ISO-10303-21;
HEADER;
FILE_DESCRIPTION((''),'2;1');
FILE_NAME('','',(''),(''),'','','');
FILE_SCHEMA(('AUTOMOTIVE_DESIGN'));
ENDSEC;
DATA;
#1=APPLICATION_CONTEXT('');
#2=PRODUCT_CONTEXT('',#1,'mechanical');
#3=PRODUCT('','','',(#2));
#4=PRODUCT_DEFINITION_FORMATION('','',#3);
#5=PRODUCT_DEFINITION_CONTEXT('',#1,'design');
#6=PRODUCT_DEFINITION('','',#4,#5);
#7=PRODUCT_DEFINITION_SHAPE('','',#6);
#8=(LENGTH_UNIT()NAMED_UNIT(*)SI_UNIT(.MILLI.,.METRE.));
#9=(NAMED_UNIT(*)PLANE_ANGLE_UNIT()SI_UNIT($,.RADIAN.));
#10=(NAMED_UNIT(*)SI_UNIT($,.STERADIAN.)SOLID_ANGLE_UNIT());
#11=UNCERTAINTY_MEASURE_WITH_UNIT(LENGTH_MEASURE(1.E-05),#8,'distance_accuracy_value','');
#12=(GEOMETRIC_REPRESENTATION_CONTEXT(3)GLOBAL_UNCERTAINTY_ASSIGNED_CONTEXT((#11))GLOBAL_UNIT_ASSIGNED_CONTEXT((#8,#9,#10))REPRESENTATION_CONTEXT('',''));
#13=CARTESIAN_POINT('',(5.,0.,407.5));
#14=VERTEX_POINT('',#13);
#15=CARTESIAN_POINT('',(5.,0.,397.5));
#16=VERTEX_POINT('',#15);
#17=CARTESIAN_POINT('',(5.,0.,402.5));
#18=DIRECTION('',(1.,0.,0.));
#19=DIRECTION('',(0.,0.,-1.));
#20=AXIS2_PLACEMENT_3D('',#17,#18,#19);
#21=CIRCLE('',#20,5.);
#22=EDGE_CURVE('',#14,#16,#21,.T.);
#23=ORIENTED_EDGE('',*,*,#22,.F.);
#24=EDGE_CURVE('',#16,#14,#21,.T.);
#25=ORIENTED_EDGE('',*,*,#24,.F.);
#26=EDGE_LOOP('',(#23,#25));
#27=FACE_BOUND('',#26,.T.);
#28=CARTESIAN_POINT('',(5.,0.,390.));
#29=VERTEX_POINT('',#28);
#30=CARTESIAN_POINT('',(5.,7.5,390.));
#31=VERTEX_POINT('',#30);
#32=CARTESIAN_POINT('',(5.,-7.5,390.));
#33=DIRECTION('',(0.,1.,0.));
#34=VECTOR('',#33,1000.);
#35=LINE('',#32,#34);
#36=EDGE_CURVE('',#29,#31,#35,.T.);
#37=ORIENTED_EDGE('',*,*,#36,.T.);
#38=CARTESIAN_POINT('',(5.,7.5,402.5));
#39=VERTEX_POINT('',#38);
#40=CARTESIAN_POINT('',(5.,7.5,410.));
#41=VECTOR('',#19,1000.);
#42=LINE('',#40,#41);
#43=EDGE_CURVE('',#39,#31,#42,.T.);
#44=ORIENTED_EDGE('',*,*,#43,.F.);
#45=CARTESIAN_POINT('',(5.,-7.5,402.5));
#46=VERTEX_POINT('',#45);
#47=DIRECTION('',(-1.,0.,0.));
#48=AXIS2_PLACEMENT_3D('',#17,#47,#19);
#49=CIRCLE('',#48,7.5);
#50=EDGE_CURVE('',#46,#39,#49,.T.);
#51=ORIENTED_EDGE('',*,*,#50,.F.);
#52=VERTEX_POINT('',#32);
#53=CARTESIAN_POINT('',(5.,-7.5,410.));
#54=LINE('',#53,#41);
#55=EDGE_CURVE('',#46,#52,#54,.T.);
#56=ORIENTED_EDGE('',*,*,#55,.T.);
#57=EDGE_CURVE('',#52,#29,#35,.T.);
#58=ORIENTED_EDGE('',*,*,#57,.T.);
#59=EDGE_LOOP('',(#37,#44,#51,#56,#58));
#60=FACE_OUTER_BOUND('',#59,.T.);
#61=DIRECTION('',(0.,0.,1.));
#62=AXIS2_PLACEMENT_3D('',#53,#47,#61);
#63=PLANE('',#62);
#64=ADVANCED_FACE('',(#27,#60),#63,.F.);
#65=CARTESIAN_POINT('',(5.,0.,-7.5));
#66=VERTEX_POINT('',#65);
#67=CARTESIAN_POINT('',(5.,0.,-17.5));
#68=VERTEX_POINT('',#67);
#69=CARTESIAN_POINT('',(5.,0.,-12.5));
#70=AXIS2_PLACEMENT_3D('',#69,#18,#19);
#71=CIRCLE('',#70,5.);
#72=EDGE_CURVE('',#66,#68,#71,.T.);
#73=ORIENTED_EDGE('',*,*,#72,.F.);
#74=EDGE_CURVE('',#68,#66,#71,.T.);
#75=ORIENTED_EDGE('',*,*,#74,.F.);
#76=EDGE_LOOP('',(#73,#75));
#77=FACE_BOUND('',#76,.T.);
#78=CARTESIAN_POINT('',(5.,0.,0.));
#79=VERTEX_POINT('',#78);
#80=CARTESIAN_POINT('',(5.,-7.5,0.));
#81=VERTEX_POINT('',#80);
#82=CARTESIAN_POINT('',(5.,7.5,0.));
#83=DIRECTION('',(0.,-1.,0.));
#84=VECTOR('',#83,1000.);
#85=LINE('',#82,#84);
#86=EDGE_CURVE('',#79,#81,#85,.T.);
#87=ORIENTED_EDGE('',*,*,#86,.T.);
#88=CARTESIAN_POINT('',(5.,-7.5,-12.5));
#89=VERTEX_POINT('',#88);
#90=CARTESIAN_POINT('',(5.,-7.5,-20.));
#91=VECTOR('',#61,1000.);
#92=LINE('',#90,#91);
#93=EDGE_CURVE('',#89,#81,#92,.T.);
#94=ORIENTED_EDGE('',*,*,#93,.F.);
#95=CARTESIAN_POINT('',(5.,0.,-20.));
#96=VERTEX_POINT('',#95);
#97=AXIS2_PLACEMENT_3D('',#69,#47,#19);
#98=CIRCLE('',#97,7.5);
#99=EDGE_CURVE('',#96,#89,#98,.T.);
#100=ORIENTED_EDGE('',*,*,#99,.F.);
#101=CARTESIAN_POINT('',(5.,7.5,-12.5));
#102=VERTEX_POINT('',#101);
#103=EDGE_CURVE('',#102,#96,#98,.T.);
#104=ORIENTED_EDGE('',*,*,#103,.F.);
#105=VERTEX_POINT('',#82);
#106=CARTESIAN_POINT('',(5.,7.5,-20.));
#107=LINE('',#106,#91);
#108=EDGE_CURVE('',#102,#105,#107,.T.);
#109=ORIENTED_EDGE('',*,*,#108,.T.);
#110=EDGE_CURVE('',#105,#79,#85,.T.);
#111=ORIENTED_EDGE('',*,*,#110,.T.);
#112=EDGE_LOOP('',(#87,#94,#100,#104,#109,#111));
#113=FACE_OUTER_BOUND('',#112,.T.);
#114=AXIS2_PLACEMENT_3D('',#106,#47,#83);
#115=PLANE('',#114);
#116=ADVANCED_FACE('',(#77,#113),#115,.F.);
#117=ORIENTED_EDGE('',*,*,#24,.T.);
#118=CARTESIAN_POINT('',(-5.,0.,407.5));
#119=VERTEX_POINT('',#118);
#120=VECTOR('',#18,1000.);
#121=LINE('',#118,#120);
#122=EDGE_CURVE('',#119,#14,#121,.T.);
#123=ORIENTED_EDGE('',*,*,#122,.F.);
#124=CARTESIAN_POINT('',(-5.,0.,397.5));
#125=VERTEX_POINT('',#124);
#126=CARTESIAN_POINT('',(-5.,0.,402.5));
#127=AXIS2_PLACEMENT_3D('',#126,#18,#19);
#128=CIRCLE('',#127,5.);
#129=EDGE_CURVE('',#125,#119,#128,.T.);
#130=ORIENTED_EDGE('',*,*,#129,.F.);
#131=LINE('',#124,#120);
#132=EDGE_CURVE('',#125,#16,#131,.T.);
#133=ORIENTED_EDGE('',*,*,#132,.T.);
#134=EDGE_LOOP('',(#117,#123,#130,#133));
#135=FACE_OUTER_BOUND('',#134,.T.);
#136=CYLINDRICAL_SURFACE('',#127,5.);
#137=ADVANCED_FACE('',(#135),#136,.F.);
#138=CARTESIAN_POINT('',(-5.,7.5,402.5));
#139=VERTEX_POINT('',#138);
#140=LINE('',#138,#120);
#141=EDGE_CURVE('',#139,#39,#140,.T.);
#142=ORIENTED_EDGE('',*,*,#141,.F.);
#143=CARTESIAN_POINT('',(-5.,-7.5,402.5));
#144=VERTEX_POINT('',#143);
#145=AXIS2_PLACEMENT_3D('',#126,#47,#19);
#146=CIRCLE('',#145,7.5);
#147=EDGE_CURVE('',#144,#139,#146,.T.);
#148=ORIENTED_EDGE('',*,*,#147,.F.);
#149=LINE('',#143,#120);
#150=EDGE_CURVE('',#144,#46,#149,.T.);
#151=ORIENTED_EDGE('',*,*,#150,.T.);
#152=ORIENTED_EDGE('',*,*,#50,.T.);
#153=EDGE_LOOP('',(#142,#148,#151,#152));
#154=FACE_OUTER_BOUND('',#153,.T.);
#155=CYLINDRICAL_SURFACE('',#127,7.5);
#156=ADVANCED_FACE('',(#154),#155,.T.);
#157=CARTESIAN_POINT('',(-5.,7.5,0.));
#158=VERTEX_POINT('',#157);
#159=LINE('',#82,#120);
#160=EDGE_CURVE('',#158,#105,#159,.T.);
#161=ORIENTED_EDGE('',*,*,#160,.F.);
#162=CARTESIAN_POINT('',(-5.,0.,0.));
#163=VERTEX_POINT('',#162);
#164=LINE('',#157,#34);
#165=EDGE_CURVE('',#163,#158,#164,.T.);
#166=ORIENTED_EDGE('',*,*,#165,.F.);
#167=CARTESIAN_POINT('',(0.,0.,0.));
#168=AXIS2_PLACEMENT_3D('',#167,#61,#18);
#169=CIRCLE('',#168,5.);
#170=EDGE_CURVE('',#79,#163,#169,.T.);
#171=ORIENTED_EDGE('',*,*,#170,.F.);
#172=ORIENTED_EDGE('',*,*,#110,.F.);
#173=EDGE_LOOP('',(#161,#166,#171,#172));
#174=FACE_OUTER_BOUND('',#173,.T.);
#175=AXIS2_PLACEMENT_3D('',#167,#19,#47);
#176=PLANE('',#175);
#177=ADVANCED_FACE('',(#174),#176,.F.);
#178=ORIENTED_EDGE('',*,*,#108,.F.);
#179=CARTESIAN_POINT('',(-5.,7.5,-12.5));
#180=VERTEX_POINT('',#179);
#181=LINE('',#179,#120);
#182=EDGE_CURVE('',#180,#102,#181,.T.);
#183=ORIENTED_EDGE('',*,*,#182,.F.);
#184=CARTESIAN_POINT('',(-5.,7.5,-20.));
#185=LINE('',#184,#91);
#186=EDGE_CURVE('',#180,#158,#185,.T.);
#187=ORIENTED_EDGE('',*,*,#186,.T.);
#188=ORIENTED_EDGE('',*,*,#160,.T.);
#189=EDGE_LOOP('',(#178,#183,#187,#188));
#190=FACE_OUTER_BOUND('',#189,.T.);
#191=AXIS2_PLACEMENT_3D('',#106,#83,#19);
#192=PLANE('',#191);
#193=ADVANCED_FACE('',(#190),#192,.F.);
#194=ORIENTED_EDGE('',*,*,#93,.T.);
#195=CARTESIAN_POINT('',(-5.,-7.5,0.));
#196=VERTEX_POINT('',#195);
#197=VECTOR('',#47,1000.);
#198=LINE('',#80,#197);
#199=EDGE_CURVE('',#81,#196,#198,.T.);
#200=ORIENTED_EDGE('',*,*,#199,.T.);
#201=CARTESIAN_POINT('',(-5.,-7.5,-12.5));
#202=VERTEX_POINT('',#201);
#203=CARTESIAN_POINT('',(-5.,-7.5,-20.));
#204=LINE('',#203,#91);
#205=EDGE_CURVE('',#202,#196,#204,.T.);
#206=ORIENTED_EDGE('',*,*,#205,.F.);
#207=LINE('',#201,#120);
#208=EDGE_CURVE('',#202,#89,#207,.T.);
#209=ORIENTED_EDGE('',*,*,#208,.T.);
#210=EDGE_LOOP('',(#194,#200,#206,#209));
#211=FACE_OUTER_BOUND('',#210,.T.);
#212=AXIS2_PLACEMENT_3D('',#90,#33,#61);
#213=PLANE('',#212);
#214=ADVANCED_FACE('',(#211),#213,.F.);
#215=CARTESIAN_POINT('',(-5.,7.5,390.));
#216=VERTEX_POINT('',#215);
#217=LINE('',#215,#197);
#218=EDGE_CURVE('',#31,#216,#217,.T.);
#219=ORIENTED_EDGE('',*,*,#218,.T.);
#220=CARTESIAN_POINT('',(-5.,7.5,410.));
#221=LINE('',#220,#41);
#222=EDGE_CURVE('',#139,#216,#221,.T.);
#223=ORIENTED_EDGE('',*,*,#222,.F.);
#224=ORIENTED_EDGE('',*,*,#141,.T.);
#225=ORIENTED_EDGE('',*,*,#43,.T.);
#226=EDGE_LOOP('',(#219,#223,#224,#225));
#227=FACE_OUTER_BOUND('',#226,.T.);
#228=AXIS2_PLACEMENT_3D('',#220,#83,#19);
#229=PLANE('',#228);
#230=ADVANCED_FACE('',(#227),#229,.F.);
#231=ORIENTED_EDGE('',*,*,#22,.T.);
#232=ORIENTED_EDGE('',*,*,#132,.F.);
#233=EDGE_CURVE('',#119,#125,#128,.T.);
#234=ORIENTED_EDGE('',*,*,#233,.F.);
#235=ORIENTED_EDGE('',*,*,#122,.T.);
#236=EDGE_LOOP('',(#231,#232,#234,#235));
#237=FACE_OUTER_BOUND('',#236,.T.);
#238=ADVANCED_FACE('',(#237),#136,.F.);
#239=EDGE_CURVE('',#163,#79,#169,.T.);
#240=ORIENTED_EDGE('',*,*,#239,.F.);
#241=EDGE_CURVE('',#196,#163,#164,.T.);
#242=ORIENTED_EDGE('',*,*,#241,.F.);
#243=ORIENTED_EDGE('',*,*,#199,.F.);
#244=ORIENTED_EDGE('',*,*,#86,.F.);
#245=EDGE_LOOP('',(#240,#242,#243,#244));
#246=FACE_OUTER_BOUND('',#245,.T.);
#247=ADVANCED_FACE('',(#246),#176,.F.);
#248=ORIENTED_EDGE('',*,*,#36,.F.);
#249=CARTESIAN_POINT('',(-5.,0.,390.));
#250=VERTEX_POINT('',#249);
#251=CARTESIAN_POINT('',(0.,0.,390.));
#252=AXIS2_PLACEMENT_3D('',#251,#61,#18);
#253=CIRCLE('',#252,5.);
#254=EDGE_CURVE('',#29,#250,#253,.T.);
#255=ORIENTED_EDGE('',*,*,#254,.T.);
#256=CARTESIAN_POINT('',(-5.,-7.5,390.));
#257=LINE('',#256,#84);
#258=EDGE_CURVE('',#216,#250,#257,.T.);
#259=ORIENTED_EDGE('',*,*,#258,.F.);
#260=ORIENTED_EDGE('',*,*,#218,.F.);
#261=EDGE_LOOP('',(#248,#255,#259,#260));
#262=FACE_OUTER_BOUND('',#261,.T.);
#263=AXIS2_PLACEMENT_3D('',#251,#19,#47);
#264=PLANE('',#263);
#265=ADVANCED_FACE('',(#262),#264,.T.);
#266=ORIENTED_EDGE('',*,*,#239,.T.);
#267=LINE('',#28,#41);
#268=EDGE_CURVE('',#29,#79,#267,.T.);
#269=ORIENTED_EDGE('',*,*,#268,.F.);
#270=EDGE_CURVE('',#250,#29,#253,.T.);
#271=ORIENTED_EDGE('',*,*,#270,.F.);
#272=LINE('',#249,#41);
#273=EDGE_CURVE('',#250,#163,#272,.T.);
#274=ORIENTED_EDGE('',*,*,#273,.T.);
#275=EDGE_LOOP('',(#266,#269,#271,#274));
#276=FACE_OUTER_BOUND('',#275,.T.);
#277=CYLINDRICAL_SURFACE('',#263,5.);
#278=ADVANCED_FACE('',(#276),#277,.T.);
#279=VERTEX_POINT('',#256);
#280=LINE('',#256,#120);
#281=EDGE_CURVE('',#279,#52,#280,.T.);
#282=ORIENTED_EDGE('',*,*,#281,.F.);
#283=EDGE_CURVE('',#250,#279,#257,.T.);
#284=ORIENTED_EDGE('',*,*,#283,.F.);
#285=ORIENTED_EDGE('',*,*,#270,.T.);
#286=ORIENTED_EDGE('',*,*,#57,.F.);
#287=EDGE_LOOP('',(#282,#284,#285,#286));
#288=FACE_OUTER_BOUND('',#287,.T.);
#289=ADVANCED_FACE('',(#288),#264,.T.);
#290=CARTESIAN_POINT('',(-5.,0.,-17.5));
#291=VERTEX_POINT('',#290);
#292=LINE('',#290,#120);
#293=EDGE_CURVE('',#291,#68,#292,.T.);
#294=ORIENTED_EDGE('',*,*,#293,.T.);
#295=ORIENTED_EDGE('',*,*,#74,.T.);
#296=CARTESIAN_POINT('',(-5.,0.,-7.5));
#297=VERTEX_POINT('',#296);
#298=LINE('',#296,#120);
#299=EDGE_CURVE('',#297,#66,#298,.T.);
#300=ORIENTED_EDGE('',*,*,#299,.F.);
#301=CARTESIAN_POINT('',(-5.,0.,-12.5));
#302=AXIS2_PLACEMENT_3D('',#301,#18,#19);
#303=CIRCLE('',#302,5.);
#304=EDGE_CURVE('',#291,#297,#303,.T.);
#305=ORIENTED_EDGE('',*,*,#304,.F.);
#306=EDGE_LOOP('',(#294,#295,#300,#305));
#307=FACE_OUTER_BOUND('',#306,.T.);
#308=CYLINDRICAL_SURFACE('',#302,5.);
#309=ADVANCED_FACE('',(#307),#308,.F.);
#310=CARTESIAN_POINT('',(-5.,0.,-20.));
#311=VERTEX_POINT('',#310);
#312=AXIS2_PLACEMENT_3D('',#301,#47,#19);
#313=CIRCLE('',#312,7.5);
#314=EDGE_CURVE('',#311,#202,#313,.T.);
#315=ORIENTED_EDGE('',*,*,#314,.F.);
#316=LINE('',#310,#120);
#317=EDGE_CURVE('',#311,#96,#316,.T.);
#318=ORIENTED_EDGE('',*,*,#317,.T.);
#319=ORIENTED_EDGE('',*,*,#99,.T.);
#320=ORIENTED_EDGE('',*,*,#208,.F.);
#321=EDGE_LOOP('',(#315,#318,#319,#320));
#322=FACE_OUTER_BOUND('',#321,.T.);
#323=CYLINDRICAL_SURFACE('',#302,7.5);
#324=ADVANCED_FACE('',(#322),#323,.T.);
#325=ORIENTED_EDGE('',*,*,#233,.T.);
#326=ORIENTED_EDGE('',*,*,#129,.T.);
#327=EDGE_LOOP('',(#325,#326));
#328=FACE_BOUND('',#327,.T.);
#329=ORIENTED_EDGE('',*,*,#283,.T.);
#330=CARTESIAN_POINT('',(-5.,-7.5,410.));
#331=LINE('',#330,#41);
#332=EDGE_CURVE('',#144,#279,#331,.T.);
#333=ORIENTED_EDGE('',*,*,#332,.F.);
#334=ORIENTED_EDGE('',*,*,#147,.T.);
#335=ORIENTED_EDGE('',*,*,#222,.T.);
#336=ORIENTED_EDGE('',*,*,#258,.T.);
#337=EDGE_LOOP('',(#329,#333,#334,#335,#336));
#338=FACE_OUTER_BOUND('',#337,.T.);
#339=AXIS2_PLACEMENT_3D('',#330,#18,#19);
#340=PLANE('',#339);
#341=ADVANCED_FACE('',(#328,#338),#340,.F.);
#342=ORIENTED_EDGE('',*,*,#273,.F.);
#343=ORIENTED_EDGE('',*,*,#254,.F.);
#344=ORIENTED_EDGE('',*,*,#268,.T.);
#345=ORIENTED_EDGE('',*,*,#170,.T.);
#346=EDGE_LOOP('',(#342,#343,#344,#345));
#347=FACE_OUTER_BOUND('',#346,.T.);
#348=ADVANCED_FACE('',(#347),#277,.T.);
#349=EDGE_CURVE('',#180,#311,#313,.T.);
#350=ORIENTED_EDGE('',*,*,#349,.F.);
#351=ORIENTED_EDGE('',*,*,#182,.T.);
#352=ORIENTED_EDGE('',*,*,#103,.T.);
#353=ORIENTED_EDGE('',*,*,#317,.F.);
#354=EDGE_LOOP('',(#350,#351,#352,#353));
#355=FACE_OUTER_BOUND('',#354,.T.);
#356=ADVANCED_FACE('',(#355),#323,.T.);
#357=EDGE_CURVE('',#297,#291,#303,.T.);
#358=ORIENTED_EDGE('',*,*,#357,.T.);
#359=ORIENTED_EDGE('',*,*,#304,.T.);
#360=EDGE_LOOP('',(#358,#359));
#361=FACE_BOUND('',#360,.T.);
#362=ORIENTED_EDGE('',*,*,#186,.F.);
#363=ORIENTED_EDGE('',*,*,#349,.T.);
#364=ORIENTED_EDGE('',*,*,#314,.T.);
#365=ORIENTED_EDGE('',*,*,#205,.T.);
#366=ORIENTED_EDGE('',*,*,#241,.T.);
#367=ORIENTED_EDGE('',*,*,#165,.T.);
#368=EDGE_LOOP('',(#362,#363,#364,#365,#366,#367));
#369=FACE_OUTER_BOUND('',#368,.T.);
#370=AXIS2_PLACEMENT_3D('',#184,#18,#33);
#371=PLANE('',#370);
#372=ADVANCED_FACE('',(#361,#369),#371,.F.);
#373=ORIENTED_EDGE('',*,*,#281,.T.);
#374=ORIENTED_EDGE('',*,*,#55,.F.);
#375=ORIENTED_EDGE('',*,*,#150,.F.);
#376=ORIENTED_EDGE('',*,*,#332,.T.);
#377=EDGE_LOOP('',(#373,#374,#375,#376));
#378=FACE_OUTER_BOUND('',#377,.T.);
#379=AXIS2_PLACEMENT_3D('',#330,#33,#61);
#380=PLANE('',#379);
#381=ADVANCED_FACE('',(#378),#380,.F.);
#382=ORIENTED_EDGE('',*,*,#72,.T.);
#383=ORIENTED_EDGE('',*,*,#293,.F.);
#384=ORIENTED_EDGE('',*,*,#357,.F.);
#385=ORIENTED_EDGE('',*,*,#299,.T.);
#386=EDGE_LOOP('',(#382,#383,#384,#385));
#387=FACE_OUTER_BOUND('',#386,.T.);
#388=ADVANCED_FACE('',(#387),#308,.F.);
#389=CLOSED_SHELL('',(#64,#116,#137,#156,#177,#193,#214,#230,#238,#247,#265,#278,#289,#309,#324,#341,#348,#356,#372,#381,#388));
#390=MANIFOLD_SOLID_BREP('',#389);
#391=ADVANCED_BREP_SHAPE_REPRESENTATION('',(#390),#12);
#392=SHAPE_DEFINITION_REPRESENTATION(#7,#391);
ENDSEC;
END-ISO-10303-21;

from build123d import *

# Parameters (mm, degrees)
SKETCH1_R           = 5
BOSS_EXTRUDE1_DEPTH = 390
SKETCH2_W           = 10
SKETCH2_H           = 15
BOSS_EXTRUDE2_DEPTH = 20
SKETCH3_W           = 10
SKETCH3_H           = 15
BOSS_EXTRUDE3_DEPTH = 20
SKETCH4_R           = 5
CUT_EXTRUDE1_DEPTH  = 411.190504522


with BuildPart() as part:
    # Sketch1 → Boss-Extrude1 (new body)
    with BuildSketch(Plane.XY):
        Circle(SKETCH1_R)
    extrude(amount=BOSS_EXTRUDE1_DEPTH)

    # Sketch2 → Boss-Extrude2 (add)
    with BuildSketch(Plane(origin=(0, 0, 0), x_dir=(-1, 0, 0), z_dir=(0, 0, -1))):
        Rectangle(SKETCH2_W, SKETCH2_H)
    extrude(amount=BOSS_EXTRUDE2_DEPTH)

    # Sketch3 → Boss-Extrude3 (add)
    with BuildSketch(Plane.XY.offset(390)):
        Rectangle(SKETCH3_W, SKETCH3_H)
    extrude(amount=BOSS_EXTRUDE3_DEPTH)

    # Sketch4 → Cut-Extrude1 (cut, through all)
    with BuildSketch(Plane(origin=(5, 0, 0), x_dir=(0, 0, -1), z_dir=(1, 0, 0))):
        with Locations((12.5, 0)):
            Circle(SKETCH4_R)
        with Locations((-402.5, 0)):
            Circle(SKETCH4_R)
        with BuildLine():
            Line((12.5, -7.5), (27.957175819, -19.344646022))
            Line((27.957175819, -19.344646022), (25.412525065, 11.111642689))
            Line((25.412525065, 11.111642689), (12.5, 7.5))
            ThreePointArc((12.5, 7.5), (20, 0), (12.5, -7.5))
        make_face()
        with BuildLine():
            Line((-402.5, 7.5), (-436.593003508, 16.998965127))
            Line((-436.593003508, 16.998965127), (-417.537871644, -29.426265233))
            Line((-417.537871644, -29.426265233), (-402.5, -7.5))
            ThreePointArc((-402.5, -7.5), (-410, 0), (-402.5, 7.5))
        make_face()
    extrude(amount=-CUT_EXTRUDE1_DEPTH, mode=Mode.SUBTRACT)


solid = part.part
